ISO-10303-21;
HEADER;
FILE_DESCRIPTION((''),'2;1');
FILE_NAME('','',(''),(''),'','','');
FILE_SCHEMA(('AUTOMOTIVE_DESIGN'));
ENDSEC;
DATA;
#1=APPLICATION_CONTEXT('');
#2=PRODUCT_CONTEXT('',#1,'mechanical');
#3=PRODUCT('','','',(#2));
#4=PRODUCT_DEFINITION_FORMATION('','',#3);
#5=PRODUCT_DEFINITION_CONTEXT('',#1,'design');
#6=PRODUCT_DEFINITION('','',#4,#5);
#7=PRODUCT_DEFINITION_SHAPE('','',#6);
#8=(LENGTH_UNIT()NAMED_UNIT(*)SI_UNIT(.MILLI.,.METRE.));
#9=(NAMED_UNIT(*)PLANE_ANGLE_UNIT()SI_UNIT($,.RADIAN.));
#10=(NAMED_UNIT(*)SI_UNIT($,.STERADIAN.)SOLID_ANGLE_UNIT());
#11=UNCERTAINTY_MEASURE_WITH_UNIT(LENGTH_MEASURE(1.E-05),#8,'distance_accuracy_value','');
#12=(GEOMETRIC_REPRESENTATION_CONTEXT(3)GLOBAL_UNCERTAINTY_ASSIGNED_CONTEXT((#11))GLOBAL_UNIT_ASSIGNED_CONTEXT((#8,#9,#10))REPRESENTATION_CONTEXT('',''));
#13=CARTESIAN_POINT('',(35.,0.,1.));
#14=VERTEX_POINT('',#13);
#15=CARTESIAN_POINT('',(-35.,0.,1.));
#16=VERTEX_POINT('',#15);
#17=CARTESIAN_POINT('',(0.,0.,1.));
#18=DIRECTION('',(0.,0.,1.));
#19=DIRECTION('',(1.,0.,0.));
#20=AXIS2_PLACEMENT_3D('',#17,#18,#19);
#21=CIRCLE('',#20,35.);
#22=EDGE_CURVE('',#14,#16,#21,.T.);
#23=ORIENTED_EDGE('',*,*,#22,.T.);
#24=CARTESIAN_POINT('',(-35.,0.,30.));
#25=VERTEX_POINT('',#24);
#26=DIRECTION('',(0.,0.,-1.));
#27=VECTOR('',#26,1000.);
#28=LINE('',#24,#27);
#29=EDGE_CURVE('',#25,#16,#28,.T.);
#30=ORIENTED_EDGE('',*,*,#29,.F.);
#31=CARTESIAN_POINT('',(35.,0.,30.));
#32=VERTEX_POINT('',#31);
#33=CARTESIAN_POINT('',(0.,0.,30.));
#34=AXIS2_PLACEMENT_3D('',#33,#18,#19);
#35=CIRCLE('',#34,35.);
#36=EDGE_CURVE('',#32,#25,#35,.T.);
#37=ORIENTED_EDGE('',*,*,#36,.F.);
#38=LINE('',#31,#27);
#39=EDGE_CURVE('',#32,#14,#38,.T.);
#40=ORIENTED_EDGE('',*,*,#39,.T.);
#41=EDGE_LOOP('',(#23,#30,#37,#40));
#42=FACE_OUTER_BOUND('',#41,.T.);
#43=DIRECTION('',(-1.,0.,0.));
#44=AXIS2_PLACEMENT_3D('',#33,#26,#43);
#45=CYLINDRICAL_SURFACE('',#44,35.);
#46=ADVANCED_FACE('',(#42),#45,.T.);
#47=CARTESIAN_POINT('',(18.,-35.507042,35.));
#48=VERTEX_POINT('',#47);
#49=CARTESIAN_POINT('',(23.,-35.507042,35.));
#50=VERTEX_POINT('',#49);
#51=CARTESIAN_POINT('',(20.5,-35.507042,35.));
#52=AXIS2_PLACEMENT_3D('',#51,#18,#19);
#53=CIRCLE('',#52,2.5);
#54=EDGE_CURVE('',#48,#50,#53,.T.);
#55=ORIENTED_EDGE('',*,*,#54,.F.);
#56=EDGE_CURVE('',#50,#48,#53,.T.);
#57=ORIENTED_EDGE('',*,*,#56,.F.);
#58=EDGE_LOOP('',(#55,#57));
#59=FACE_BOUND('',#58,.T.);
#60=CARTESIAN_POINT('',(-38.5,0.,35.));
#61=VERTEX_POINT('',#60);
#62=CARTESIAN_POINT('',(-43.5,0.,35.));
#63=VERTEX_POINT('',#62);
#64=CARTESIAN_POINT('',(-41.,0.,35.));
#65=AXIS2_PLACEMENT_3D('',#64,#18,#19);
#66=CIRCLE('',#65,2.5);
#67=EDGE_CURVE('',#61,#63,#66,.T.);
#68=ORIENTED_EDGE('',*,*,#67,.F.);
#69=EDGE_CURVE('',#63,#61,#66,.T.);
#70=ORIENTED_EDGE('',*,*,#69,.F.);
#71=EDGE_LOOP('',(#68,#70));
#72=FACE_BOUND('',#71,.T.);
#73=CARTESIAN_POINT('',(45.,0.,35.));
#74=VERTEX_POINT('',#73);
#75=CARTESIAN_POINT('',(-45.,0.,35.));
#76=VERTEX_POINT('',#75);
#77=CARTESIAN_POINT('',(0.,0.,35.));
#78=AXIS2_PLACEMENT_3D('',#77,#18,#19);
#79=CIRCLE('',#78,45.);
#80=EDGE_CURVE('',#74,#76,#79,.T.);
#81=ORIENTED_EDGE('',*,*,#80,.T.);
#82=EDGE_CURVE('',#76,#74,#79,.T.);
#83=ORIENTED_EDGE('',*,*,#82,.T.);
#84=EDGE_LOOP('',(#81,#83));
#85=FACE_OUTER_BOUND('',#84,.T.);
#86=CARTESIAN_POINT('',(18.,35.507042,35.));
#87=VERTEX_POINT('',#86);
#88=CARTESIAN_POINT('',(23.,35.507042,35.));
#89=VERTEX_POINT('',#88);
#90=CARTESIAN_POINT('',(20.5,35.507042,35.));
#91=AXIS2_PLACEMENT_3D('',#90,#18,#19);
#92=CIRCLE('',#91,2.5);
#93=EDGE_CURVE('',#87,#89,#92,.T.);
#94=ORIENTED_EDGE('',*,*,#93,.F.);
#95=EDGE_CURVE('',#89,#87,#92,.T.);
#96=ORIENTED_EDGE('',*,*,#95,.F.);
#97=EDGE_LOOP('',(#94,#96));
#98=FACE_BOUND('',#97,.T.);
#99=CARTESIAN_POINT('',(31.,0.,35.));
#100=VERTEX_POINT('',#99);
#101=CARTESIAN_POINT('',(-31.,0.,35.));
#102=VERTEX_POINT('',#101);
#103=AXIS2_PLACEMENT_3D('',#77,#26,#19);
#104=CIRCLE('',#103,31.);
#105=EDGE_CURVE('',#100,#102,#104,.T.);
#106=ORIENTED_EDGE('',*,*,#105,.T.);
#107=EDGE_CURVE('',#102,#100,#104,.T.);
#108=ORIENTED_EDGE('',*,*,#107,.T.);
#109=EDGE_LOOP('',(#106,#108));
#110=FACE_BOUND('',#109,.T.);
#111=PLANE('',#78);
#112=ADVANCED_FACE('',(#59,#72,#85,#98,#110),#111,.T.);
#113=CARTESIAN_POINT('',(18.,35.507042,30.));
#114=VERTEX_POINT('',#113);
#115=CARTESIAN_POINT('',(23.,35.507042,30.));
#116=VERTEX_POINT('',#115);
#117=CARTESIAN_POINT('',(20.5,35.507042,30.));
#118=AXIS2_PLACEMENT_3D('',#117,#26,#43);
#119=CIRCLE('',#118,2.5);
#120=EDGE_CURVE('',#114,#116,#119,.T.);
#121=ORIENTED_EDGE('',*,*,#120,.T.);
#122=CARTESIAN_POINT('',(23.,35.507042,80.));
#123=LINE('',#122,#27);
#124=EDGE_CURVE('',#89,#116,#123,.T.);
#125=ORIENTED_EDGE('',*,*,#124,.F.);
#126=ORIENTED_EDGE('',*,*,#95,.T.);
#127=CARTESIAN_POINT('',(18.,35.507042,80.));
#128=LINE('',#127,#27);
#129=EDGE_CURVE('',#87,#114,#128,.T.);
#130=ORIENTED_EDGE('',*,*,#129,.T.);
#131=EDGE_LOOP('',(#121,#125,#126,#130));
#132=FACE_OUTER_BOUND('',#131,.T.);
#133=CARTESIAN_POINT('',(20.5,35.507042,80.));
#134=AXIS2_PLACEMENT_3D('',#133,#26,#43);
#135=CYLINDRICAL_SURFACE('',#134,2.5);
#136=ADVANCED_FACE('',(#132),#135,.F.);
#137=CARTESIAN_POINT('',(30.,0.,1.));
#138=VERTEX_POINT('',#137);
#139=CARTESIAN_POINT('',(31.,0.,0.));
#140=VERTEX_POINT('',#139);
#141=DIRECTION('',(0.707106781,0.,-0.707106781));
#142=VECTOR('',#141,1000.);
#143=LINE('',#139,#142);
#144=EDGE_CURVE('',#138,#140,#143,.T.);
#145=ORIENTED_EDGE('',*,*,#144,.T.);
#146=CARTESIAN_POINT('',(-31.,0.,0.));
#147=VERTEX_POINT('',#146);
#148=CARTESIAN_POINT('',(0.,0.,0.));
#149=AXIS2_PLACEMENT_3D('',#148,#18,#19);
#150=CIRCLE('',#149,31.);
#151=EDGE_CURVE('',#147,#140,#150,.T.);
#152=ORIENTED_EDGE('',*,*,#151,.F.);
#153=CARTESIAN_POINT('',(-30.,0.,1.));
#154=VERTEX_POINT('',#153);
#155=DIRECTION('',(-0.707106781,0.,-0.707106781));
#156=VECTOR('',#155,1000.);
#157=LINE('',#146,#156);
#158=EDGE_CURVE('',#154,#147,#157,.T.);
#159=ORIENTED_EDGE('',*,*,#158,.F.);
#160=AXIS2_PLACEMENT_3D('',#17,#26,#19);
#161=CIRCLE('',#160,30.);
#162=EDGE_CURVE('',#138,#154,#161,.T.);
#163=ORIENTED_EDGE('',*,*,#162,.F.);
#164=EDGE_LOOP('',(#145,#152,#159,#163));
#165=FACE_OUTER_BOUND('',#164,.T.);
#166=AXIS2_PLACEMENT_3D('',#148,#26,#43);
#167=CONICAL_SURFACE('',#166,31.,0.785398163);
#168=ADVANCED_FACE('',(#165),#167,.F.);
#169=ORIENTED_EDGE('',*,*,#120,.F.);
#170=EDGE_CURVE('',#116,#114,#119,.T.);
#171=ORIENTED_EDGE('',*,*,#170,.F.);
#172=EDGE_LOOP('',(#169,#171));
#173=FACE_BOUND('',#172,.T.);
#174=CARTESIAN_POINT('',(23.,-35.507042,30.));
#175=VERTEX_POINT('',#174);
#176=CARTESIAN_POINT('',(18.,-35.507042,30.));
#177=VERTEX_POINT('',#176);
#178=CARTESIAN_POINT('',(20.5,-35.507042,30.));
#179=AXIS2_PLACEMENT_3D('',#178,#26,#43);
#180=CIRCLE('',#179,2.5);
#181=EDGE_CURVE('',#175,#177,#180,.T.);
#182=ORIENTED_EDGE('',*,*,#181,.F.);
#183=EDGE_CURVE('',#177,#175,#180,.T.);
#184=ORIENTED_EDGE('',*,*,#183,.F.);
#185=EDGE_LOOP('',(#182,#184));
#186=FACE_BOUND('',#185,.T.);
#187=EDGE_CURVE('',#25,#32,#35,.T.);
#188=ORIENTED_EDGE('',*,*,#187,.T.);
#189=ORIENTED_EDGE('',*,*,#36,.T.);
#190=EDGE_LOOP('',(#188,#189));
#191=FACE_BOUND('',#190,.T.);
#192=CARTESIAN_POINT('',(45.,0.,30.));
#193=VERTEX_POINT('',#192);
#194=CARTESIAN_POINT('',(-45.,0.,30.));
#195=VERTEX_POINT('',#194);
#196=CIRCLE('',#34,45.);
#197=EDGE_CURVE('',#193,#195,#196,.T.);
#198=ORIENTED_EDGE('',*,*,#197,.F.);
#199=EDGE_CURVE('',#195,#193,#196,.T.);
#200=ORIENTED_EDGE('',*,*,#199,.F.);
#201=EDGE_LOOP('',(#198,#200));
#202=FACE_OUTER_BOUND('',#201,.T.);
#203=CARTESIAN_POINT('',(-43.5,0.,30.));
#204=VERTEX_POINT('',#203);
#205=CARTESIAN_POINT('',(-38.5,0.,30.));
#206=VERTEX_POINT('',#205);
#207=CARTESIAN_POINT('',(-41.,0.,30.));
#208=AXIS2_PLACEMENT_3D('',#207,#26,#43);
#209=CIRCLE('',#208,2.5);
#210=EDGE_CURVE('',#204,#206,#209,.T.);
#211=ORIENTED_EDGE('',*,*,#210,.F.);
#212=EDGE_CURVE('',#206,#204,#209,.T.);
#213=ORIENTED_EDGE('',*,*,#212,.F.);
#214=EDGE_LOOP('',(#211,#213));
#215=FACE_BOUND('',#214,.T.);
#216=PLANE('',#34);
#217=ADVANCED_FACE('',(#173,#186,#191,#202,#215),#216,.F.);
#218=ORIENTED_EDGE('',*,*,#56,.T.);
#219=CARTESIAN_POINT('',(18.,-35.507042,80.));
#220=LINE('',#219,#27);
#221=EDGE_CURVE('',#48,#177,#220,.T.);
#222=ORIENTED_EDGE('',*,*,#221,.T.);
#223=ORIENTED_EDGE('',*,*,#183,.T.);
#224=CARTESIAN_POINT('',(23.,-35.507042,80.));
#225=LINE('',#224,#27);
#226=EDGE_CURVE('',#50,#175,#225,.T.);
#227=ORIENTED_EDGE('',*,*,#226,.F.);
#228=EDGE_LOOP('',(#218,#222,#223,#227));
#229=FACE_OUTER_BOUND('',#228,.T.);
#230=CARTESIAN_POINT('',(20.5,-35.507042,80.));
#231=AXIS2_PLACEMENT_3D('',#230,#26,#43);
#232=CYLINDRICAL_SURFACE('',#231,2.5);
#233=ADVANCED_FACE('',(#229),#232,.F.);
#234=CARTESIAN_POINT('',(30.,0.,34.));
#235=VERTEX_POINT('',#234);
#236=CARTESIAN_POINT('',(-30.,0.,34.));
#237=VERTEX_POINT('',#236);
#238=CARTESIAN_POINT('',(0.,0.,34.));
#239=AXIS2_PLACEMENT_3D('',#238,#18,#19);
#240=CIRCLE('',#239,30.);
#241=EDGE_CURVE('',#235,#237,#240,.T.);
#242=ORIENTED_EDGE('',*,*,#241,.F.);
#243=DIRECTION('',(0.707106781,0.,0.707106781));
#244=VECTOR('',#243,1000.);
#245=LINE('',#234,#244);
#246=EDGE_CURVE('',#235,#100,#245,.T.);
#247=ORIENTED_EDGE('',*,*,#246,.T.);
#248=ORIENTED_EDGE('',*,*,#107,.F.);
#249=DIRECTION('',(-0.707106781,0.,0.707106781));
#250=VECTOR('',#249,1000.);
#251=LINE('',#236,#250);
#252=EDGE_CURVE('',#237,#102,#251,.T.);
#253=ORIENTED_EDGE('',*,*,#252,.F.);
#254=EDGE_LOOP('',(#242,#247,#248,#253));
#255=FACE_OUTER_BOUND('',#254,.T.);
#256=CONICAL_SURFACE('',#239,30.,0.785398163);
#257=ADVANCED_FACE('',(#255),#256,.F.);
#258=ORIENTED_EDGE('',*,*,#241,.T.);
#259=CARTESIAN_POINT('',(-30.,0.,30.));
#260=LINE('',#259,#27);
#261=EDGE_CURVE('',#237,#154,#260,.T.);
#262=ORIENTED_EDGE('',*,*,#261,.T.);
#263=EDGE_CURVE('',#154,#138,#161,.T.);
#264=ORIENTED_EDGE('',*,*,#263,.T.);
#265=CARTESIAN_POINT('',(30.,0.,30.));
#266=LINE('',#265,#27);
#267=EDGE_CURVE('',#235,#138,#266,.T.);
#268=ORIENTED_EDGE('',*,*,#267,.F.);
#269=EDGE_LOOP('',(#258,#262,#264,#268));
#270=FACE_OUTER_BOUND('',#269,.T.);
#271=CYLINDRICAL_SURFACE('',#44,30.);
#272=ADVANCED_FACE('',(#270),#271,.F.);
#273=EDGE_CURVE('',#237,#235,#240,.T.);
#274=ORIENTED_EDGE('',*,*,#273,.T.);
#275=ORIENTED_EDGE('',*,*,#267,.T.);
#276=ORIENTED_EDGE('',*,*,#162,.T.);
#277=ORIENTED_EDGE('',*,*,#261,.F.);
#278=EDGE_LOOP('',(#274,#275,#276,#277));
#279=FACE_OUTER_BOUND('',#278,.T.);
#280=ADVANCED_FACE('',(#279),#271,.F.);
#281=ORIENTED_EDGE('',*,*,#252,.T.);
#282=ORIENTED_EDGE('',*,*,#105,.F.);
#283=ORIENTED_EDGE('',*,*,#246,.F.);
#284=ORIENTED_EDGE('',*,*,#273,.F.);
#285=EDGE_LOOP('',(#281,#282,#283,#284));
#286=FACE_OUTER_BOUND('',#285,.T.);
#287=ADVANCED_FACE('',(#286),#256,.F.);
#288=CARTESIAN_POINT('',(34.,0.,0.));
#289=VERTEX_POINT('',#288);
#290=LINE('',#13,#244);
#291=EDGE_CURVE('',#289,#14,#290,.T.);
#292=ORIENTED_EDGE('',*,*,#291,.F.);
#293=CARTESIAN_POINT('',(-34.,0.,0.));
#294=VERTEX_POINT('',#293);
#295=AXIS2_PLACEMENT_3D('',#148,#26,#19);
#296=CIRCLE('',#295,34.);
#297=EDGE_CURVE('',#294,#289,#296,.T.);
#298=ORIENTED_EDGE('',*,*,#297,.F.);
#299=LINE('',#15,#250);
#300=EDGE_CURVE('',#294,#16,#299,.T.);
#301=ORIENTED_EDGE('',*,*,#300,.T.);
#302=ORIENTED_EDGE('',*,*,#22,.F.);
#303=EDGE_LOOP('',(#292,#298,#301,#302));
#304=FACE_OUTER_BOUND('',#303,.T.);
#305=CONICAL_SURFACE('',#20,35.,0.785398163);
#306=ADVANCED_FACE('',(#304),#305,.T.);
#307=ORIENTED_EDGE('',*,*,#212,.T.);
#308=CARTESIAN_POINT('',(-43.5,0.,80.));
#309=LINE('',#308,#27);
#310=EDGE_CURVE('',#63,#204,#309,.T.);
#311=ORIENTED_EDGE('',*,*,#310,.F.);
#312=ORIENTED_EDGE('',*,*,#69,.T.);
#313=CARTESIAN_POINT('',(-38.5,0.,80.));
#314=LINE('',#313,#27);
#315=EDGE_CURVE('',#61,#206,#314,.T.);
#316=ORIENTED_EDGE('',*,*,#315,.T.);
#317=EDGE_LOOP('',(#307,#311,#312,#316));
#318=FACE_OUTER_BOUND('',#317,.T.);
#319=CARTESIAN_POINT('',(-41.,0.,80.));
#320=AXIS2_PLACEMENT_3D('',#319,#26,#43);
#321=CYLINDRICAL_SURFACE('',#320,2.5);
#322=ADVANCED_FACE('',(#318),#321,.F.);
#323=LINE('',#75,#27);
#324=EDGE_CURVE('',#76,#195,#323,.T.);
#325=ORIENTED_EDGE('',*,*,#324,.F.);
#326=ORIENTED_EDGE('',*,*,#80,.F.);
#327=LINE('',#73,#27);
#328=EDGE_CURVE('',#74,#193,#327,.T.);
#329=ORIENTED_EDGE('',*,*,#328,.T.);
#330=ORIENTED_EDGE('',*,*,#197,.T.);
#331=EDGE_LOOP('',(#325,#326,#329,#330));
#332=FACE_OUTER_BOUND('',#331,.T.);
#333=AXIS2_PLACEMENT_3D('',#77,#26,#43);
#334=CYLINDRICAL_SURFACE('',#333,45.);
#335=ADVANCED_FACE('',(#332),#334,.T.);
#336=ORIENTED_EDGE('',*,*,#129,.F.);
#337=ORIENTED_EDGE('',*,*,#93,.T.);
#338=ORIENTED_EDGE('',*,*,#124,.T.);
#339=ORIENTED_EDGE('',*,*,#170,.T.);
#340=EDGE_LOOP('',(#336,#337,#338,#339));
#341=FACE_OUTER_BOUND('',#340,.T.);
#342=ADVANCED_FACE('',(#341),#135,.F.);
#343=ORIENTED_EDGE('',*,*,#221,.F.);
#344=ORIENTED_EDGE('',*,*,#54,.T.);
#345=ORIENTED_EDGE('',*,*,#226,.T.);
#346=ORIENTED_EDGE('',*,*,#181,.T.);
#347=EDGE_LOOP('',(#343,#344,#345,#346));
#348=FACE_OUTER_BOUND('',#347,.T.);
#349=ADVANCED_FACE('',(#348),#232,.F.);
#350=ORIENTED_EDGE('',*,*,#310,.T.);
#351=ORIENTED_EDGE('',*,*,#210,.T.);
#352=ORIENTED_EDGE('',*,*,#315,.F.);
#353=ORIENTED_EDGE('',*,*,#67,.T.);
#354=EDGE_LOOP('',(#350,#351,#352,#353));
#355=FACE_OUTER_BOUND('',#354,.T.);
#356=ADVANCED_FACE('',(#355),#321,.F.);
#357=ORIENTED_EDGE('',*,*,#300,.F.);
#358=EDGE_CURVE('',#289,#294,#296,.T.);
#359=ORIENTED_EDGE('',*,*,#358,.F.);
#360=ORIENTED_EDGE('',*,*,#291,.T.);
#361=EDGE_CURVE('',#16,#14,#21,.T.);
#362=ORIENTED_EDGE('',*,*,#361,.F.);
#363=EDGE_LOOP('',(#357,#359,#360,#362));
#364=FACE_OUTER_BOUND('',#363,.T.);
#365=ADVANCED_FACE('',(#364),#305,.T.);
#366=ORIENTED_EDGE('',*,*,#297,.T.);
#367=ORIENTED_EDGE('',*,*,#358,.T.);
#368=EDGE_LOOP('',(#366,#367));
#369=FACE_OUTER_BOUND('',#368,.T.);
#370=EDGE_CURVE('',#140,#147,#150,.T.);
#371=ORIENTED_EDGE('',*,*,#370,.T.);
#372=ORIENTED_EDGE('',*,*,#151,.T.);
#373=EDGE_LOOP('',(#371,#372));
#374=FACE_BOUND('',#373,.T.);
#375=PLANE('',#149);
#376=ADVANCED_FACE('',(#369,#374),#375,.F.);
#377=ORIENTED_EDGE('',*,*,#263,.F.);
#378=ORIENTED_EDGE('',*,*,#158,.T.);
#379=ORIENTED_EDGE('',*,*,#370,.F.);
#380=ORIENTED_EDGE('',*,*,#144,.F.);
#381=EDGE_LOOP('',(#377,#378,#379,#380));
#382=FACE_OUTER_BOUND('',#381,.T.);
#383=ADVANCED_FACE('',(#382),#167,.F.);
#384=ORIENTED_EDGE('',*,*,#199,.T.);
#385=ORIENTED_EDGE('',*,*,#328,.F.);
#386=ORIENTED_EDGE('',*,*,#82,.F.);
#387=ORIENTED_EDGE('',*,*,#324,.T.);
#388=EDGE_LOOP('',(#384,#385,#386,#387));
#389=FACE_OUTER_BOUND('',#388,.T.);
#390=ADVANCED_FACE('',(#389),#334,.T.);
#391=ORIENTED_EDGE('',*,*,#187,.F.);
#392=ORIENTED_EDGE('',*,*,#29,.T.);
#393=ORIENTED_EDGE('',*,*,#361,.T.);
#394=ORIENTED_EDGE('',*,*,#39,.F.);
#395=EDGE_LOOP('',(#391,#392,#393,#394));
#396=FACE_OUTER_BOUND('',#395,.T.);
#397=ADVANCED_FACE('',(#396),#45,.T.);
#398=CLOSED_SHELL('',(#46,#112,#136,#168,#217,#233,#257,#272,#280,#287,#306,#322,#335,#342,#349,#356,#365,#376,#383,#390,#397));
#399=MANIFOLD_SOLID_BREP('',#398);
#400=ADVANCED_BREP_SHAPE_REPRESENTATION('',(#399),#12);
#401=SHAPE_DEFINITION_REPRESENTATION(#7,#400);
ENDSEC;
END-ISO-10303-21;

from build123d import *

# Parameters (mm, degrees)
SKETCH1_R           = 35
SKETCH1_R_2         = 30
BOSS_EXTRUDE1_DEPTH = 30
SKETCH2_R           = 45
SKETCH2_R_2         = 30
BOSS_EXTRUDE2_DEPTH = 5
SKETCH3_R           = 2.5
CUT_EXTRUDE1_DEPTH  = 50
CHAMFER1_SIZE       = 1


with BuildPart() as part:
    # Sketch1 → Boss-Extrude1 (new body)
    with BuildSketch(Plane.XY):
        Circle(SKETCH1_R)
        Circle(SKETCH1_R_2, mode=Mode.SUBTRACT)
    extrude(amount=BOSS_EXTRUDE1_DEPTH)

    # Sketch2 → Boss-Extrude2 (add)
    with BuildSketch(Plane.XY.offset(30)):
        Circle(SKETCH2_R)
        Circle(SKETCH2_R_2, mode=Mode.SUBTRACT)
    extrude(amount=BOSS_EXTRUDE2_DEPTH)

    # Sketch3 → Cut-Extrude1 (cut)
    with BuildSketch(Plane(origin=(0, 0, 30), x_dir=(-1, 0, 0), z_dir=(0, 0, -1))):
        with Locations((41, 0)):
            Circle(SKETCH3_R)
        with Locations((-20.5, -35.507041555)):
            Circle(SKETCH3_R)
        with Locations((-20.5, 35.507041555)):
            Circle(SKETCH3_R)
    extrude(amount=-CUT_EXTRUDE1_DEPTH, mode=Mode.SUBTRACT)

    # Chamfer1
    chamfer1_edges = [part.edges().sort_by_distance(p)[0] for p in [
        (-30, 0, 35),
        (-35, 0, 0),
        (-30, 0, 0),
    ]]
    chamfer(chamfer1_edges, length=CHAMFER1_SIZE)


solid = part.part
